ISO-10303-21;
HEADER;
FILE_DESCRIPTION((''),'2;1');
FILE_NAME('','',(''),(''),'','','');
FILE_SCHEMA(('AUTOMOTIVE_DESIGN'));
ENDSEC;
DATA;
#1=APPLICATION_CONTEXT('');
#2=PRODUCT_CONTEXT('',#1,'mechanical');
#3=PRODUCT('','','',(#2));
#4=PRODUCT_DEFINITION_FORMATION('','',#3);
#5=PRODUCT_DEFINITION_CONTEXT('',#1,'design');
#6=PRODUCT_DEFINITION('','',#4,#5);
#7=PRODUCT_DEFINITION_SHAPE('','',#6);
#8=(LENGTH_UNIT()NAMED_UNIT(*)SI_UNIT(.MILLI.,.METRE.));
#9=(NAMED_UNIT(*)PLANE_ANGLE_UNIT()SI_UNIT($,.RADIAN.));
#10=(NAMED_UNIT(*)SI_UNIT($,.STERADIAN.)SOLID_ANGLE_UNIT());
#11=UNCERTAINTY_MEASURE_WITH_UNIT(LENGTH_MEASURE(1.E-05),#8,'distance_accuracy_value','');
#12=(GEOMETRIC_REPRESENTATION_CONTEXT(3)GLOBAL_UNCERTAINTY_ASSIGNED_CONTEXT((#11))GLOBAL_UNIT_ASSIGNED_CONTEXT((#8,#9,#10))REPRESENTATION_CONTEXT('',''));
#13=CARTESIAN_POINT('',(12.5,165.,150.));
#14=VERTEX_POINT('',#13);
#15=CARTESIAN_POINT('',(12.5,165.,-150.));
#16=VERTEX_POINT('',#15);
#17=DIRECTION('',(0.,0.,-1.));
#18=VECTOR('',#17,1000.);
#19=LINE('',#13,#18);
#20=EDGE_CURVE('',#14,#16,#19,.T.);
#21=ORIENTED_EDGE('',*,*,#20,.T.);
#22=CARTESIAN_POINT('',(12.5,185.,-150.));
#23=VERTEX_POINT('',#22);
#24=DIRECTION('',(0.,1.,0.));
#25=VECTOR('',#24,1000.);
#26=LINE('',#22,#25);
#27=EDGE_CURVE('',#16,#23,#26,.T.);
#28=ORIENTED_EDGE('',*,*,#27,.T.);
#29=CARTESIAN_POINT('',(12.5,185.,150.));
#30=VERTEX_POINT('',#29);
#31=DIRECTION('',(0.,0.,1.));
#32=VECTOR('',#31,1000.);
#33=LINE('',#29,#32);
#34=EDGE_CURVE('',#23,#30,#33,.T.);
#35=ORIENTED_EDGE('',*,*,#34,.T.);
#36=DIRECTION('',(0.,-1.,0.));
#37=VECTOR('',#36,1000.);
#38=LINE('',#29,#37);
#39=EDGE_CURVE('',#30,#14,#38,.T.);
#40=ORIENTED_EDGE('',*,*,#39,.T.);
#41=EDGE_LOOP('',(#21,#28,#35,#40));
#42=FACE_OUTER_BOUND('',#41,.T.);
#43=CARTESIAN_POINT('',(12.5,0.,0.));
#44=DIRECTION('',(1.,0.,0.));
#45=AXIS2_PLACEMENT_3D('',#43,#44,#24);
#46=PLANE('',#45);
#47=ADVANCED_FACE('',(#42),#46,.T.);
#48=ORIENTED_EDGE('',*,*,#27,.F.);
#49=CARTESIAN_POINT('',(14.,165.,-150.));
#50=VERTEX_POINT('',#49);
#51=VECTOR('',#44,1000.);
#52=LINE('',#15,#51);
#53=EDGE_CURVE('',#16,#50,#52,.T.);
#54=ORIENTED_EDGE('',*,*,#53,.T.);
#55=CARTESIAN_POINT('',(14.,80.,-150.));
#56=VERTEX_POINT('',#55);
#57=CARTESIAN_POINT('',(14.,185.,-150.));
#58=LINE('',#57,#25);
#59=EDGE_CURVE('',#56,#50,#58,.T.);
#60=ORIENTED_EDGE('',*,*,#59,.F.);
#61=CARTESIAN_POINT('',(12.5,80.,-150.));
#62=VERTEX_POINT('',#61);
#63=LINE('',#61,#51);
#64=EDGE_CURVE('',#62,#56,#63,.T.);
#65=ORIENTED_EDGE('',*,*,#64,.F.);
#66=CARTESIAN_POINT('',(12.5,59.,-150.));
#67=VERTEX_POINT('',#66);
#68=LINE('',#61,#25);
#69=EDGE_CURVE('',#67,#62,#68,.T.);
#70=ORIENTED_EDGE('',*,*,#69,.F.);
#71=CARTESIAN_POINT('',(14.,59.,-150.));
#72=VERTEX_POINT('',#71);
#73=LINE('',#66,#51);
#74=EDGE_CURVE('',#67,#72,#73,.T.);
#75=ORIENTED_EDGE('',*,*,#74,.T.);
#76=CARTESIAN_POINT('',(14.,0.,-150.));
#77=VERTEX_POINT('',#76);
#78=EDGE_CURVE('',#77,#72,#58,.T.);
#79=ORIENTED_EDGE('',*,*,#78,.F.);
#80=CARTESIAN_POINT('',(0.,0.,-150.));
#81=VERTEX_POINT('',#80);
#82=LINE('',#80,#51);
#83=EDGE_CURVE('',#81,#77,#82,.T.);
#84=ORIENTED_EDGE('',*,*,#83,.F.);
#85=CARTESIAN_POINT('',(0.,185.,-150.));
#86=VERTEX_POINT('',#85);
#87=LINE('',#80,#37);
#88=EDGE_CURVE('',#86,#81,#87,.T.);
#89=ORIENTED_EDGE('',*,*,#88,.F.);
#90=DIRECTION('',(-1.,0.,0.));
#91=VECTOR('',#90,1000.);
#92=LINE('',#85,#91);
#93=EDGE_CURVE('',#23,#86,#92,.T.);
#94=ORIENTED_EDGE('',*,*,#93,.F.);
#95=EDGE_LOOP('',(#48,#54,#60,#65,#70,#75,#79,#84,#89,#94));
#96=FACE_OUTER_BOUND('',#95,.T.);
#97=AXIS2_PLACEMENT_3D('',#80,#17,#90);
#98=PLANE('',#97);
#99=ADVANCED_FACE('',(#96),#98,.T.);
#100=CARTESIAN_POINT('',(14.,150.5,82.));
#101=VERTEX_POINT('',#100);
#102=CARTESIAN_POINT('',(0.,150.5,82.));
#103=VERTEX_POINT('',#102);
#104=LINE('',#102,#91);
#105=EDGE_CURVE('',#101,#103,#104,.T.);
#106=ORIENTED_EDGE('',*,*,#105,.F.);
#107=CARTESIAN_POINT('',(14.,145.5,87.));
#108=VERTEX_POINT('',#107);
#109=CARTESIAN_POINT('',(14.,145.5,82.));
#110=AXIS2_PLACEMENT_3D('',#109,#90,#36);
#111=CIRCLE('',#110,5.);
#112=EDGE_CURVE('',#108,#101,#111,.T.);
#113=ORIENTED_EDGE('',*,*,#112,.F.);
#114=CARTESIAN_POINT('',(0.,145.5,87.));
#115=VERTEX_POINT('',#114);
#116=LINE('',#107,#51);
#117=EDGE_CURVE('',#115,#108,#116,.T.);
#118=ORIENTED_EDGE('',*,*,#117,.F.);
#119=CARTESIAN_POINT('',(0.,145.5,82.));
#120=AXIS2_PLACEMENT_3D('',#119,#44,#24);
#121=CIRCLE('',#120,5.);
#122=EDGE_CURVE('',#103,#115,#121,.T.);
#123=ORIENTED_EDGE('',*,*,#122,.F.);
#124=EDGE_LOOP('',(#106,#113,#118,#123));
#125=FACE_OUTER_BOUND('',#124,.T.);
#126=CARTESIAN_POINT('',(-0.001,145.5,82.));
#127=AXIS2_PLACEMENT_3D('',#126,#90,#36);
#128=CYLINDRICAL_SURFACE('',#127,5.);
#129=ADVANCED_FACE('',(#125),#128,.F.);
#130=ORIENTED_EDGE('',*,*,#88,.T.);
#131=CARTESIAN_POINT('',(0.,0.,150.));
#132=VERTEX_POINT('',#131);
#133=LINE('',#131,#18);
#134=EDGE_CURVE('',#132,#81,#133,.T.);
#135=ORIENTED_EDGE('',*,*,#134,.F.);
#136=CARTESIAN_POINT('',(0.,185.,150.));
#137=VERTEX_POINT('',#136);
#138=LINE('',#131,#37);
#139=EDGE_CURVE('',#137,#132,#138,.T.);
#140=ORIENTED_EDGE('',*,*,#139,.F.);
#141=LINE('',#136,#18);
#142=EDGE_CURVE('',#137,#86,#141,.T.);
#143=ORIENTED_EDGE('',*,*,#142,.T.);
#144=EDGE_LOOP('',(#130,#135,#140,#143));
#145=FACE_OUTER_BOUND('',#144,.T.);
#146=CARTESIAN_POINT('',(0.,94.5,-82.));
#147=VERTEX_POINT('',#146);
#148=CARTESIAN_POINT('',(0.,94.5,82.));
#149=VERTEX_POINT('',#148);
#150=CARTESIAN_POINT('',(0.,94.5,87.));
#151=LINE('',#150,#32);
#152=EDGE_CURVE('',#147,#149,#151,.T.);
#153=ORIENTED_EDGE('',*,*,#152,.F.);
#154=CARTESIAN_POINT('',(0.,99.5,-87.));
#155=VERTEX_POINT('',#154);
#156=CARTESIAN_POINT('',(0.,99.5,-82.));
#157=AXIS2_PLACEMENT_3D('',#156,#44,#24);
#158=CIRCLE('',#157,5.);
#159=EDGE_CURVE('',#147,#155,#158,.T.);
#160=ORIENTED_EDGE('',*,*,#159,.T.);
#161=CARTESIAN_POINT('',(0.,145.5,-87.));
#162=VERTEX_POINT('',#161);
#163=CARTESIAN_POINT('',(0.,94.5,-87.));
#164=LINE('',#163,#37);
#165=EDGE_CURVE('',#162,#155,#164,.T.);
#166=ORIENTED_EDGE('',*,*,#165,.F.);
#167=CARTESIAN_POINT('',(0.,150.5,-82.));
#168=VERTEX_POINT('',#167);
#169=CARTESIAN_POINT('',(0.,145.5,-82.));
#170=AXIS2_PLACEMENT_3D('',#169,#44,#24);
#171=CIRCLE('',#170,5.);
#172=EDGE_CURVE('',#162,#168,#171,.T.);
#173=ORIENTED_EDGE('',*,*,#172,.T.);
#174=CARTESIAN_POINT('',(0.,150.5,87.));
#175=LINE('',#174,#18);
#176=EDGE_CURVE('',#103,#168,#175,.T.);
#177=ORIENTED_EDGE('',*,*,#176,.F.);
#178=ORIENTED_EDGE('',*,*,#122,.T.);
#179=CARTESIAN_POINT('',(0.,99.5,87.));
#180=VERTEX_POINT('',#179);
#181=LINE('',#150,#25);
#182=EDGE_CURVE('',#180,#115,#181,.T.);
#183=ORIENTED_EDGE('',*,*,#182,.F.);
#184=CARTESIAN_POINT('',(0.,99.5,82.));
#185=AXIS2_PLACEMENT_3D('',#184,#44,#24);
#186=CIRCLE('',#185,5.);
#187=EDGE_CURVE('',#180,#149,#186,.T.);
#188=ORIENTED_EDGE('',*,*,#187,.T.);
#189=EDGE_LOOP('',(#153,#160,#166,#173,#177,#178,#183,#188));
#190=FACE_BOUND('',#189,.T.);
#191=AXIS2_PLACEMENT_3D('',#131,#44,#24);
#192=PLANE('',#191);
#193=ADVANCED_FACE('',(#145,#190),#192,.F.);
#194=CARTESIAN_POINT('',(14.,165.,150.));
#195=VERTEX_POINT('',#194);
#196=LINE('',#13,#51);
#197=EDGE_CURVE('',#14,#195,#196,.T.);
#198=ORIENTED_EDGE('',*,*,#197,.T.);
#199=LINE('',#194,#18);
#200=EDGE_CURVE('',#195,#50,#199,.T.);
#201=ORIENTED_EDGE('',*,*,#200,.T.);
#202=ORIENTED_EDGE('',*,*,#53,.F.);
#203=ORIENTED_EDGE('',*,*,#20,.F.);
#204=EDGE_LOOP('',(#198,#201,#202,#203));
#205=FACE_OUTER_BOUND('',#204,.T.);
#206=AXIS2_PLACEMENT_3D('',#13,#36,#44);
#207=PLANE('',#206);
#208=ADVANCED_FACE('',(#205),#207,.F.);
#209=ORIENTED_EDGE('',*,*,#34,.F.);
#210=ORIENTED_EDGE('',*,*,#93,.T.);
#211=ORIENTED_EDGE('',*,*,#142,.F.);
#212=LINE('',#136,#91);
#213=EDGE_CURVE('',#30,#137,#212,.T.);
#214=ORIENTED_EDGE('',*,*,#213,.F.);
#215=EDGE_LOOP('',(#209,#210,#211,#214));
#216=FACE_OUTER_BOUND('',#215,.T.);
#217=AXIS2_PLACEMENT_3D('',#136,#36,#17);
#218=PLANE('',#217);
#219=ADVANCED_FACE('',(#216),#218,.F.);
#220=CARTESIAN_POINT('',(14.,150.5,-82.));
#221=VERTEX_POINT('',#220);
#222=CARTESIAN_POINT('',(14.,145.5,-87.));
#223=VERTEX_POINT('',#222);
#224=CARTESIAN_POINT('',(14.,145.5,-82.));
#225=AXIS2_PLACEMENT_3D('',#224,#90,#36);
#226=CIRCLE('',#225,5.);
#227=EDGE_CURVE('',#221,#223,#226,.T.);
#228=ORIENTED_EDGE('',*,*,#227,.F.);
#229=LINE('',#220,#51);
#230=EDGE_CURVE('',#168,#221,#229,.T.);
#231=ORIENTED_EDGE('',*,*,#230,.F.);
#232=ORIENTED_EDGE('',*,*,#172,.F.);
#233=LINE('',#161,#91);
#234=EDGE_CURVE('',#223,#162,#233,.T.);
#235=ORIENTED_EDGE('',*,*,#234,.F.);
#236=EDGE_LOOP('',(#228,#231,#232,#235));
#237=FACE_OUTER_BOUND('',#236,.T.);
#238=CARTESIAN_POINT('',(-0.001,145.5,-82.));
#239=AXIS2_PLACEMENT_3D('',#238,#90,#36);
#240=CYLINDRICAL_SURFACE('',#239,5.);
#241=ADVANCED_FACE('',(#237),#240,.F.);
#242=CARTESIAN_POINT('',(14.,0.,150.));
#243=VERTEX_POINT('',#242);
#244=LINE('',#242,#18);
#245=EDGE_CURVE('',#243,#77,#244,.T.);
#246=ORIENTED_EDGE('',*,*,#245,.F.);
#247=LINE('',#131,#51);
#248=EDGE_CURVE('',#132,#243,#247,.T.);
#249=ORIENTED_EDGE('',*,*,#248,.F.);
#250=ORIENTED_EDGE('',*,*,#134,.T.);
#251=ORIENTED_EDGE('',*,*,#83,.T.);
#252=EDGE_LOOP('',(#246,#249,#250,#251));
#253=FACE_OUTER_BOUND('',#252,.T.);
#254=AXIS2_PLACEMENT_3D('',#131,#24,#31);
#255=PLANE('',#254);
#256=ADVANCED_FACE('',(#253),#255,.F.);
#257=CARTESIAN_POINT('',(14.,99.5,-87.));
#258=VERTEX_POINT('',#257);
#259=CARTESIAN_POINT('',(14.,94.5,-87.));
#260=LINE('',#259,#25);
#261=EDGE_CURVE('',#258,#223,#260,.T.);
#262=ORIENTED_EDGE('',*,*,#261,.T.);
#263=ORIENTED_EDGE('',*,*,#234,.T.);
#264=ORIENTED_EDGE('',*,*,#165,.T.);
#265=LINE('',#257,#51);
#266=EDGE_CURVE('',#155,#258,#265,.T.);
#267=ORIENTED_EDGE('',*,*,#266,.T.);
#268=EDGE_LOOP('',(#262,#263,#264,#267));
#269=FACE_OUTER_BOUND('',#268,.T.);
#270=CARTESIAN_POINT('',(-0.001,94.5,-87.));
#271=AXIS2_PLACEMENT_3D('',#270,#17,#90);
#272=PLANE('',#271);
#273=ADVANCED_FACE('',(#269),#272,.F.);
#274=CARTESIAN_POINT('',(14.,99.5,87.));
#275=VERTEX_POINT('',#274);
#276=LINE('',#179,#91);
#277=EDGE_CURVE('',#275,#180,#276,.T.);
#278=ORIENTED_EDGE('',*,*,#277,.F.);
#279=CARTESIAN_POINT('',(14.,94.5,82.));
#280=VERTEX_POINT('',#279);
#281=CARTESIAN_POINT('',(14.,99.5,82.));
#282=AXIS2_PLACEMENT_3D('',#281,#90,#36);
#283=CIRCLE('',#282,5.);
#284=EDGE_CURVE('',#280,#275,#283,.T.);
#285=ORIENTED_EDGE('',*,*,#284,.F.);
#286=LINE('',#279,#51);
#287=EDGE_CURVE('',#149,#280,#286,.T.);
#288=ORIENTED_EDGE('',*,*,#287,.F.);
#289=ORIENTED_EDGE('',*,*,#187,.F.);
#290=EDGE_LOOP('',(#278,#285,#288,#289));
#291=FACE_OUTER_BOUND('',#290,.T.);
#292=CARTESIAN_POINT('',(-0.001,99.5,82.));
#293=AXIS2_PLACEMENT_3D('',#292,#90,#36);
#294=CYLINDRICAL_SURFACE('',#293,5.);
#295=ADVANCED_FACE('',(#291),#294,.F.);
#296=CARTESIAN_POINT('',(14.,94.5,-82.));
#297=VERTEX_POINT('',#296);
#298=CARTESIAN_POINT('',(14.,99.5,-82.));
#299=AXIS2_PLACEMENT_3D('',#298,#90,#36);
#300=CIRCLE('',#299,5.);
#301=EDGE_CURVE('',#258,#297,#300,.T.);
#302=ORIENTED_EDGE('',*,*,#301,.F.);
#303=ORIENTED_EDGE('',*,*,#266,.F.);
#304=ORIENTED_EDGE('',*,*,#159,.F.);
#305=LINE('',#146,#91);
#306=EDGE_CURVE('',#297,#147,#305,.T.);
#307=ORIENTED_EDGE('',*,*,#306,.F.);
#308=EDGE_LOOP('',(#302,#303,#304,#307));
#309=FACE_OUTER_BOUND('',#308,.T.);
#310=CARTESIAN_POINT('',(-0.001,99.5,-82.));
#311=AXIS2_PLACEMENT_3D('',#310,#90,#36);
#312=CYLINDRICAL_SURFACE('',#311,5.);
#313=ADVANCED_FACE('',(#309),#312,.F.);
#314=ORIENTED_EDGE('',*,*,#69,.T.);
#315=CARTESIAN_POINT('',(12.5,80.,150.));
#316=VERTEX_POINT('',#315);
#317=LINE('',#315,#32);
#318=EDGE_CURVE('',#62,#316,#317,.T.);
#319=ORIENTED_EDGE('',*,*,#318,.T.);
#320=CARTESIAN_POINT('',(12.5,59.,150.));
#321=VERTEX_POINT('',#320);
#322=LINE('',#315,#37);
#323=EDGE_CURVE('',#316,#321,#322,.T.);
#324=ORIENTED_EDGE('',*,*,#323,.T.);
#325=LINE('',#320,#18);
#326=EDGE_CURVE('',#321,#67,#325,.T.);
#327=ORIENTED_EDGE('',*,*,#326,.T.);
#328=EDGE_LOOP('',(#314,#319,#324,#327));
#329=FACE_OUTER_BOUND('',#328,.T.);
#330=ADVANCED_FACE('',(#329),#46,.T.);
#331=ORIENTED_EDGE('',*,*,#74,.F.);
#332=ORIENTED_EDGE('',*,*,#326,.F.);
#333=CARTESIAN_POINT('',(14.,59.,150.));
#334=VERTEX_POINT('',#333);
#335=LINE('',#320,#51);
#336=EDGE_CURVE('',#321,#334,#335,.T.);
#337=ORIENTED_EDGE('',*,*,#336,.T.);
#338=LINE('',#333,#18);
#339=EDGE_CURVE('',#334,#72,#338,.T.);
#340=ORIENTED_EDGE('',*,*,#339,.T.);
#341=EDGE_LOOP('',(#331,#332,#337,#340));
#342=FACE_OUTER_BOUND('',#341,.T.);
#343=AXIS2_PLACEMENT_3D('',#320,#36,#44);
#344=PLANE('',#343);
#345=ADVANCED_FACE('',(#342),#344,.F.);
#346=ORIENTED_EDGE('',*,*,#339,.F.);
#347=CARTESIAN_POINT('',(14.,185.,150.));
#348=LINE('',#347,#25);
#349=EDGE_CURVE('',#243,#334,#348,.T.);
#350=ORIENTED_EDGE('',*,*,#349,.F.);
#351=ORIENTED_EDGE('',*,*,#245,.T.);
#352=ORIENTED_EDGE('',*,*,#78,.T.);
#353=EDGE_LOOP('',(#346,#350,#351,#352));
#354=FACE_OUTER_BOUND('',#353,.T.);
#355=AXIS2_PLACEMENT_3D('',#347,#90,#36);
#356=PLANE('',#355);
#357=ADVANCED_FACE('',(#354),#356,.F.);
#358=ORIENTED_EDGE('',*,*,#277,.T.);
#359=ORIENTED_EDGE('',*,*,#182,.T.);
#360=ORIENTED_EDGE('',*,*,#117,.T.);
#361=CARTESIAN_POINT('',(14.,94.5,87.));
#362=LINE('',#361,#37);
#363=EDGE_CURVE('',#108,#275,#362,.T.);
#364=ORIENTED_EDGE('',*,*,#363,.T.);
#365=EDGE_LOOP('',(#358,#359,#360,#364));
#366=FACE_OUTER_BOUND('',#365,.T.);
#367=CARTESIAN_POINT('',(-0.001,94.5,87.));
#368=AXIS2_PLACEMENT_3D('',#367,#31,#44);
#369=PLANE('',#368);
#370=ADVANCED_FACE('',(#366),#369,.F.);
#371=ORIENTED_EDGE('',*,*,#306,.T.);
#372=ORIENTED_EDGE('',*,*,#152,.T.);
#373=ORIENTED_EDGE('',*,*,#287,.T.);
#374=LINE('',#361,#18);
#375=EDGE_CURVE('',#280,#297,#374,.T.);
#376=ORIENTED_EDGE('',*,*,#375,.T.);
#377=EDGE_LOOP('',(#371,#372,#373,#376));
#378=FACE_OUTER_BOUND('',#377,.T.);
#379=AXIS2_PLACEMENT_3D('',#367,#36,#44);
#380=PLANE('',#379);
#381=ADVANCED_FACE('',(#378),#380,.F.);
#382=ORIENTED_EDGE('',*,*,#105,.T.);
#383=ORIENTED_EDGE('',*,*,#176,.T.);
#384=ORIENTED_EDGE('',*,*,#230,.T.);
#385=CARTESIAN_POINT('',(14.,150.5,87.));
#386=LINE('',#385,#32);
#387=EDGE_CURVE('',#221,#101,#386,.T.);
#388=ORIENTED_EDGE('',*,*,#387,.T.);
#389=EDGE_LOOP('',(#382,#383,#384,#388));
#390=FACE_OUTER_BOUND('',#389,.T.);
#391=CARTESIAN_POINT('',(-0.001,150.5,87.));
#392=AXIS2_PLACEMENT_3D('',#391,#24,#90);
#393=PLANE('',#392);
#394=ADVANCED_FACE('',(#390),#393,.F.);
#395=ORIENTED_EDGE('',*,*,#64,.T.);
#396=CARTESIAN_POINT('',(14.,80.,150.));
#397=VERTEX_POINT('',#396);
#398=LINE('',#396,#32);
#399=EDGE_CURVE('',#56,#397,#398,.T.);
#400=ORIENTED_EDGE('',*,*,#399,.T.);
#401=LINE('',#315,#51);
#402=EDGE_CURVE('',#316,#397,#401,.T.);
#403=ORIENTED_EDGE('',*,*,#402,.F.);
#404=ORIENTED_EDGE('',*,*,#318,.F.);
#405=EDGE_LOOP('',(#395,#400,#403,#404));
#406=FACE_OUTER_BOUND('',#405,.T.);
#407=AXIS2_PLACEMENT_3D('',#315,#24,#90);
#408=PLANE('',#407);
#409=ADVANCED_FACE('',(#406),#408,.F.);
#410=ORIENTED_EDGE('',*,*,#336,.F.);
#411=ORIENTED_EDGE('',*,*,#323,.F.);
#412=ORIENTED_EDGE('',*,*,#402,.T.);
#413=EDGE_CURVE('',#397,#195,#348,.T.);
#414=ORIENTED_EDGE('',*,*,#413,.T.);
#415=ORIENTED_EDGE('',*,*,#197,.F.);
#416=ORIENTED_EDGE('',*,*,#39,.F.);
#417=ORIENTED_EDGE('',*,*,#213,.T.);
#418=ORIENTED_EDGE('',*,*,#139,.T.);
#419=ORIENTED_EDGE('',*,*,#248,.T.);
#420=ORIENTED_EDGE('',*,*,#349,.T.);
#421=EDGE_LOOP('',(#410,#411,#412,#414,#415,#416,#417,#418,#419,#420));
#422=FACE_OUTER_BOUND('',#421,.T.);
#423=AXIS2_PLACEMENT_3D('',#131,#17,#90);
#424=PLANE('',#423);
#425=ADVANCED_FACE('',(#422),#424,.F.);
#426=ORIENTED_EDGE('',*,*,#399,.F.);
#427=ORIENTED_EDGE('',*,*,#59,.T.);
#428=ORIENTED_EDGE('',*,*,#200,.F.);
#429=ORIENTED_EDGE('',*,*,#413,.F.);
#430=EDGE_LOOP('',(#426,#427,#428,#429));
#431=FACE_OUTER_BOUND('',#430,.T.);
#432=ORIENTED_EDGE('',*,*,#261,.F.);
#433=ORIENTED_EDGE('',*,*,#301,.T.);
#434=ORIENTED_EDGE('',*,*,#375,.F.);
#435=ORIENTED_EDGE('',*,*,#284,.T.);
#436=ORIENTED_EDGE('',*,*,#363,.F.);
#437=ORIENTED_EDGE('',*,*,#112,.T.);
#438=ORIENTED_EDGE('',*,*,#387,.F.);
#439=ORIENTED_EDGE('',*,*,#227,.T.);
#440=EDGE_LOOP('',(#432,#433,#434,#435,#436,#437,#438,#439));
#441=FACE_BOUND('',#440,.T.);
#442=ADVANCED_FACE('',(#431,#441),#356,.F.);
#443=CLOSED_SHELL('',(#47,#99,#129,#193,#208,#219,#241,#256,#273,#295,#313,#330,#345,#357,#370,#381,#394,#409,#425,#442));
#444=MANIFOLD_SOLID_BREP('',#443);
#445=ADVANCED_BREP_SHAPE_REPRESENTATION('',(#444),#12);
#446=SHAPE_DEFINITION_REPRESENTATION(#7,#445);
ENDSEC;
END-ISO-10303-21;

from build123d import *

# Parameters (mm, degrees)
SKETCH_1_W          = 14
SKETCH_1_H          = 185
EXTRUDE_1_DEPTH     = 150
SKETCH_2_W          = 300
SKETCH_2_H          = 20
SKETCH_2_H_2        = 21
CUT_EXTRUDE_1_DEPTH = 1.5
CUT_EXTRUDE_2_REACH = 240.581
SKETCH_3_W          = 174
SKETCH_3_H          = 56
FILLET_1_R          = 5


with BuildPart() as part:
    # 草图1 → 凸台-拉伸1 (new, symmetric)
    with BuildSketch(Plane.XY):
        with Locations((7, 92.5)):
            Rectangle(SKETCH_1_W, SKETCH_1_H)
    extrude(amount=EXTRUDE_1_DEPTH, both=True)

    # 草图2 → 切除-拉伸1 (cut)
    with BuildSketch(Plane(origin=(14, 0, 0), x_dir=(0, 0, -1), z_dir=(1, 0, 0))):
        with Locations((0, 175)):
            Rectangle(SKETCH_2_W, SKETCH_2_H)
        with Locations((0, 69.5)):
            Rectangle(SKETCH_2_W, SKETCH_2_H_2)
    extrude(amount=-CUT_EXTRUDE_1_DEPTH, mode=Mode.SUBTRACT)

    # 草图3 → 切除-拉伸2 (cut, up to next)
    with BuildSketch(Plane(origin=(14, 0, 0), x_dir=(0, 0, -1), z_dir=(1, 0, 0)), mode=Mode.PRIVATE) as cut_extrude_2_sk1:
        with Locations((0, 122.5)):
            Rectangle(SKETCH_3_W, SKETCH_3_H)
    cut_extrude_2_tool1 = extrude(cut_extrude_2_sk1.sketch, amount=-CUT_EXTRUDE_2_REACH, mode=Mode.PRIVATE) & part.part
    add(cut_extrude_2_tool1.solids().sort_by_distance((14, 122.5, 0))[0], mode=Mode.SUBTRACT)

    # 圆角1
    fillet_1_edges = [part.edges().sort_by_distance(p)[0] for p in [
        (7, 150.5, -87),
        (7, 94.5, -87),
        (7, 94.5, 87),
        (7, 150.5, 87),
    ]]
    fillet(fillet_1_edges, radius=FILLET_1_R)


solid = part.part
